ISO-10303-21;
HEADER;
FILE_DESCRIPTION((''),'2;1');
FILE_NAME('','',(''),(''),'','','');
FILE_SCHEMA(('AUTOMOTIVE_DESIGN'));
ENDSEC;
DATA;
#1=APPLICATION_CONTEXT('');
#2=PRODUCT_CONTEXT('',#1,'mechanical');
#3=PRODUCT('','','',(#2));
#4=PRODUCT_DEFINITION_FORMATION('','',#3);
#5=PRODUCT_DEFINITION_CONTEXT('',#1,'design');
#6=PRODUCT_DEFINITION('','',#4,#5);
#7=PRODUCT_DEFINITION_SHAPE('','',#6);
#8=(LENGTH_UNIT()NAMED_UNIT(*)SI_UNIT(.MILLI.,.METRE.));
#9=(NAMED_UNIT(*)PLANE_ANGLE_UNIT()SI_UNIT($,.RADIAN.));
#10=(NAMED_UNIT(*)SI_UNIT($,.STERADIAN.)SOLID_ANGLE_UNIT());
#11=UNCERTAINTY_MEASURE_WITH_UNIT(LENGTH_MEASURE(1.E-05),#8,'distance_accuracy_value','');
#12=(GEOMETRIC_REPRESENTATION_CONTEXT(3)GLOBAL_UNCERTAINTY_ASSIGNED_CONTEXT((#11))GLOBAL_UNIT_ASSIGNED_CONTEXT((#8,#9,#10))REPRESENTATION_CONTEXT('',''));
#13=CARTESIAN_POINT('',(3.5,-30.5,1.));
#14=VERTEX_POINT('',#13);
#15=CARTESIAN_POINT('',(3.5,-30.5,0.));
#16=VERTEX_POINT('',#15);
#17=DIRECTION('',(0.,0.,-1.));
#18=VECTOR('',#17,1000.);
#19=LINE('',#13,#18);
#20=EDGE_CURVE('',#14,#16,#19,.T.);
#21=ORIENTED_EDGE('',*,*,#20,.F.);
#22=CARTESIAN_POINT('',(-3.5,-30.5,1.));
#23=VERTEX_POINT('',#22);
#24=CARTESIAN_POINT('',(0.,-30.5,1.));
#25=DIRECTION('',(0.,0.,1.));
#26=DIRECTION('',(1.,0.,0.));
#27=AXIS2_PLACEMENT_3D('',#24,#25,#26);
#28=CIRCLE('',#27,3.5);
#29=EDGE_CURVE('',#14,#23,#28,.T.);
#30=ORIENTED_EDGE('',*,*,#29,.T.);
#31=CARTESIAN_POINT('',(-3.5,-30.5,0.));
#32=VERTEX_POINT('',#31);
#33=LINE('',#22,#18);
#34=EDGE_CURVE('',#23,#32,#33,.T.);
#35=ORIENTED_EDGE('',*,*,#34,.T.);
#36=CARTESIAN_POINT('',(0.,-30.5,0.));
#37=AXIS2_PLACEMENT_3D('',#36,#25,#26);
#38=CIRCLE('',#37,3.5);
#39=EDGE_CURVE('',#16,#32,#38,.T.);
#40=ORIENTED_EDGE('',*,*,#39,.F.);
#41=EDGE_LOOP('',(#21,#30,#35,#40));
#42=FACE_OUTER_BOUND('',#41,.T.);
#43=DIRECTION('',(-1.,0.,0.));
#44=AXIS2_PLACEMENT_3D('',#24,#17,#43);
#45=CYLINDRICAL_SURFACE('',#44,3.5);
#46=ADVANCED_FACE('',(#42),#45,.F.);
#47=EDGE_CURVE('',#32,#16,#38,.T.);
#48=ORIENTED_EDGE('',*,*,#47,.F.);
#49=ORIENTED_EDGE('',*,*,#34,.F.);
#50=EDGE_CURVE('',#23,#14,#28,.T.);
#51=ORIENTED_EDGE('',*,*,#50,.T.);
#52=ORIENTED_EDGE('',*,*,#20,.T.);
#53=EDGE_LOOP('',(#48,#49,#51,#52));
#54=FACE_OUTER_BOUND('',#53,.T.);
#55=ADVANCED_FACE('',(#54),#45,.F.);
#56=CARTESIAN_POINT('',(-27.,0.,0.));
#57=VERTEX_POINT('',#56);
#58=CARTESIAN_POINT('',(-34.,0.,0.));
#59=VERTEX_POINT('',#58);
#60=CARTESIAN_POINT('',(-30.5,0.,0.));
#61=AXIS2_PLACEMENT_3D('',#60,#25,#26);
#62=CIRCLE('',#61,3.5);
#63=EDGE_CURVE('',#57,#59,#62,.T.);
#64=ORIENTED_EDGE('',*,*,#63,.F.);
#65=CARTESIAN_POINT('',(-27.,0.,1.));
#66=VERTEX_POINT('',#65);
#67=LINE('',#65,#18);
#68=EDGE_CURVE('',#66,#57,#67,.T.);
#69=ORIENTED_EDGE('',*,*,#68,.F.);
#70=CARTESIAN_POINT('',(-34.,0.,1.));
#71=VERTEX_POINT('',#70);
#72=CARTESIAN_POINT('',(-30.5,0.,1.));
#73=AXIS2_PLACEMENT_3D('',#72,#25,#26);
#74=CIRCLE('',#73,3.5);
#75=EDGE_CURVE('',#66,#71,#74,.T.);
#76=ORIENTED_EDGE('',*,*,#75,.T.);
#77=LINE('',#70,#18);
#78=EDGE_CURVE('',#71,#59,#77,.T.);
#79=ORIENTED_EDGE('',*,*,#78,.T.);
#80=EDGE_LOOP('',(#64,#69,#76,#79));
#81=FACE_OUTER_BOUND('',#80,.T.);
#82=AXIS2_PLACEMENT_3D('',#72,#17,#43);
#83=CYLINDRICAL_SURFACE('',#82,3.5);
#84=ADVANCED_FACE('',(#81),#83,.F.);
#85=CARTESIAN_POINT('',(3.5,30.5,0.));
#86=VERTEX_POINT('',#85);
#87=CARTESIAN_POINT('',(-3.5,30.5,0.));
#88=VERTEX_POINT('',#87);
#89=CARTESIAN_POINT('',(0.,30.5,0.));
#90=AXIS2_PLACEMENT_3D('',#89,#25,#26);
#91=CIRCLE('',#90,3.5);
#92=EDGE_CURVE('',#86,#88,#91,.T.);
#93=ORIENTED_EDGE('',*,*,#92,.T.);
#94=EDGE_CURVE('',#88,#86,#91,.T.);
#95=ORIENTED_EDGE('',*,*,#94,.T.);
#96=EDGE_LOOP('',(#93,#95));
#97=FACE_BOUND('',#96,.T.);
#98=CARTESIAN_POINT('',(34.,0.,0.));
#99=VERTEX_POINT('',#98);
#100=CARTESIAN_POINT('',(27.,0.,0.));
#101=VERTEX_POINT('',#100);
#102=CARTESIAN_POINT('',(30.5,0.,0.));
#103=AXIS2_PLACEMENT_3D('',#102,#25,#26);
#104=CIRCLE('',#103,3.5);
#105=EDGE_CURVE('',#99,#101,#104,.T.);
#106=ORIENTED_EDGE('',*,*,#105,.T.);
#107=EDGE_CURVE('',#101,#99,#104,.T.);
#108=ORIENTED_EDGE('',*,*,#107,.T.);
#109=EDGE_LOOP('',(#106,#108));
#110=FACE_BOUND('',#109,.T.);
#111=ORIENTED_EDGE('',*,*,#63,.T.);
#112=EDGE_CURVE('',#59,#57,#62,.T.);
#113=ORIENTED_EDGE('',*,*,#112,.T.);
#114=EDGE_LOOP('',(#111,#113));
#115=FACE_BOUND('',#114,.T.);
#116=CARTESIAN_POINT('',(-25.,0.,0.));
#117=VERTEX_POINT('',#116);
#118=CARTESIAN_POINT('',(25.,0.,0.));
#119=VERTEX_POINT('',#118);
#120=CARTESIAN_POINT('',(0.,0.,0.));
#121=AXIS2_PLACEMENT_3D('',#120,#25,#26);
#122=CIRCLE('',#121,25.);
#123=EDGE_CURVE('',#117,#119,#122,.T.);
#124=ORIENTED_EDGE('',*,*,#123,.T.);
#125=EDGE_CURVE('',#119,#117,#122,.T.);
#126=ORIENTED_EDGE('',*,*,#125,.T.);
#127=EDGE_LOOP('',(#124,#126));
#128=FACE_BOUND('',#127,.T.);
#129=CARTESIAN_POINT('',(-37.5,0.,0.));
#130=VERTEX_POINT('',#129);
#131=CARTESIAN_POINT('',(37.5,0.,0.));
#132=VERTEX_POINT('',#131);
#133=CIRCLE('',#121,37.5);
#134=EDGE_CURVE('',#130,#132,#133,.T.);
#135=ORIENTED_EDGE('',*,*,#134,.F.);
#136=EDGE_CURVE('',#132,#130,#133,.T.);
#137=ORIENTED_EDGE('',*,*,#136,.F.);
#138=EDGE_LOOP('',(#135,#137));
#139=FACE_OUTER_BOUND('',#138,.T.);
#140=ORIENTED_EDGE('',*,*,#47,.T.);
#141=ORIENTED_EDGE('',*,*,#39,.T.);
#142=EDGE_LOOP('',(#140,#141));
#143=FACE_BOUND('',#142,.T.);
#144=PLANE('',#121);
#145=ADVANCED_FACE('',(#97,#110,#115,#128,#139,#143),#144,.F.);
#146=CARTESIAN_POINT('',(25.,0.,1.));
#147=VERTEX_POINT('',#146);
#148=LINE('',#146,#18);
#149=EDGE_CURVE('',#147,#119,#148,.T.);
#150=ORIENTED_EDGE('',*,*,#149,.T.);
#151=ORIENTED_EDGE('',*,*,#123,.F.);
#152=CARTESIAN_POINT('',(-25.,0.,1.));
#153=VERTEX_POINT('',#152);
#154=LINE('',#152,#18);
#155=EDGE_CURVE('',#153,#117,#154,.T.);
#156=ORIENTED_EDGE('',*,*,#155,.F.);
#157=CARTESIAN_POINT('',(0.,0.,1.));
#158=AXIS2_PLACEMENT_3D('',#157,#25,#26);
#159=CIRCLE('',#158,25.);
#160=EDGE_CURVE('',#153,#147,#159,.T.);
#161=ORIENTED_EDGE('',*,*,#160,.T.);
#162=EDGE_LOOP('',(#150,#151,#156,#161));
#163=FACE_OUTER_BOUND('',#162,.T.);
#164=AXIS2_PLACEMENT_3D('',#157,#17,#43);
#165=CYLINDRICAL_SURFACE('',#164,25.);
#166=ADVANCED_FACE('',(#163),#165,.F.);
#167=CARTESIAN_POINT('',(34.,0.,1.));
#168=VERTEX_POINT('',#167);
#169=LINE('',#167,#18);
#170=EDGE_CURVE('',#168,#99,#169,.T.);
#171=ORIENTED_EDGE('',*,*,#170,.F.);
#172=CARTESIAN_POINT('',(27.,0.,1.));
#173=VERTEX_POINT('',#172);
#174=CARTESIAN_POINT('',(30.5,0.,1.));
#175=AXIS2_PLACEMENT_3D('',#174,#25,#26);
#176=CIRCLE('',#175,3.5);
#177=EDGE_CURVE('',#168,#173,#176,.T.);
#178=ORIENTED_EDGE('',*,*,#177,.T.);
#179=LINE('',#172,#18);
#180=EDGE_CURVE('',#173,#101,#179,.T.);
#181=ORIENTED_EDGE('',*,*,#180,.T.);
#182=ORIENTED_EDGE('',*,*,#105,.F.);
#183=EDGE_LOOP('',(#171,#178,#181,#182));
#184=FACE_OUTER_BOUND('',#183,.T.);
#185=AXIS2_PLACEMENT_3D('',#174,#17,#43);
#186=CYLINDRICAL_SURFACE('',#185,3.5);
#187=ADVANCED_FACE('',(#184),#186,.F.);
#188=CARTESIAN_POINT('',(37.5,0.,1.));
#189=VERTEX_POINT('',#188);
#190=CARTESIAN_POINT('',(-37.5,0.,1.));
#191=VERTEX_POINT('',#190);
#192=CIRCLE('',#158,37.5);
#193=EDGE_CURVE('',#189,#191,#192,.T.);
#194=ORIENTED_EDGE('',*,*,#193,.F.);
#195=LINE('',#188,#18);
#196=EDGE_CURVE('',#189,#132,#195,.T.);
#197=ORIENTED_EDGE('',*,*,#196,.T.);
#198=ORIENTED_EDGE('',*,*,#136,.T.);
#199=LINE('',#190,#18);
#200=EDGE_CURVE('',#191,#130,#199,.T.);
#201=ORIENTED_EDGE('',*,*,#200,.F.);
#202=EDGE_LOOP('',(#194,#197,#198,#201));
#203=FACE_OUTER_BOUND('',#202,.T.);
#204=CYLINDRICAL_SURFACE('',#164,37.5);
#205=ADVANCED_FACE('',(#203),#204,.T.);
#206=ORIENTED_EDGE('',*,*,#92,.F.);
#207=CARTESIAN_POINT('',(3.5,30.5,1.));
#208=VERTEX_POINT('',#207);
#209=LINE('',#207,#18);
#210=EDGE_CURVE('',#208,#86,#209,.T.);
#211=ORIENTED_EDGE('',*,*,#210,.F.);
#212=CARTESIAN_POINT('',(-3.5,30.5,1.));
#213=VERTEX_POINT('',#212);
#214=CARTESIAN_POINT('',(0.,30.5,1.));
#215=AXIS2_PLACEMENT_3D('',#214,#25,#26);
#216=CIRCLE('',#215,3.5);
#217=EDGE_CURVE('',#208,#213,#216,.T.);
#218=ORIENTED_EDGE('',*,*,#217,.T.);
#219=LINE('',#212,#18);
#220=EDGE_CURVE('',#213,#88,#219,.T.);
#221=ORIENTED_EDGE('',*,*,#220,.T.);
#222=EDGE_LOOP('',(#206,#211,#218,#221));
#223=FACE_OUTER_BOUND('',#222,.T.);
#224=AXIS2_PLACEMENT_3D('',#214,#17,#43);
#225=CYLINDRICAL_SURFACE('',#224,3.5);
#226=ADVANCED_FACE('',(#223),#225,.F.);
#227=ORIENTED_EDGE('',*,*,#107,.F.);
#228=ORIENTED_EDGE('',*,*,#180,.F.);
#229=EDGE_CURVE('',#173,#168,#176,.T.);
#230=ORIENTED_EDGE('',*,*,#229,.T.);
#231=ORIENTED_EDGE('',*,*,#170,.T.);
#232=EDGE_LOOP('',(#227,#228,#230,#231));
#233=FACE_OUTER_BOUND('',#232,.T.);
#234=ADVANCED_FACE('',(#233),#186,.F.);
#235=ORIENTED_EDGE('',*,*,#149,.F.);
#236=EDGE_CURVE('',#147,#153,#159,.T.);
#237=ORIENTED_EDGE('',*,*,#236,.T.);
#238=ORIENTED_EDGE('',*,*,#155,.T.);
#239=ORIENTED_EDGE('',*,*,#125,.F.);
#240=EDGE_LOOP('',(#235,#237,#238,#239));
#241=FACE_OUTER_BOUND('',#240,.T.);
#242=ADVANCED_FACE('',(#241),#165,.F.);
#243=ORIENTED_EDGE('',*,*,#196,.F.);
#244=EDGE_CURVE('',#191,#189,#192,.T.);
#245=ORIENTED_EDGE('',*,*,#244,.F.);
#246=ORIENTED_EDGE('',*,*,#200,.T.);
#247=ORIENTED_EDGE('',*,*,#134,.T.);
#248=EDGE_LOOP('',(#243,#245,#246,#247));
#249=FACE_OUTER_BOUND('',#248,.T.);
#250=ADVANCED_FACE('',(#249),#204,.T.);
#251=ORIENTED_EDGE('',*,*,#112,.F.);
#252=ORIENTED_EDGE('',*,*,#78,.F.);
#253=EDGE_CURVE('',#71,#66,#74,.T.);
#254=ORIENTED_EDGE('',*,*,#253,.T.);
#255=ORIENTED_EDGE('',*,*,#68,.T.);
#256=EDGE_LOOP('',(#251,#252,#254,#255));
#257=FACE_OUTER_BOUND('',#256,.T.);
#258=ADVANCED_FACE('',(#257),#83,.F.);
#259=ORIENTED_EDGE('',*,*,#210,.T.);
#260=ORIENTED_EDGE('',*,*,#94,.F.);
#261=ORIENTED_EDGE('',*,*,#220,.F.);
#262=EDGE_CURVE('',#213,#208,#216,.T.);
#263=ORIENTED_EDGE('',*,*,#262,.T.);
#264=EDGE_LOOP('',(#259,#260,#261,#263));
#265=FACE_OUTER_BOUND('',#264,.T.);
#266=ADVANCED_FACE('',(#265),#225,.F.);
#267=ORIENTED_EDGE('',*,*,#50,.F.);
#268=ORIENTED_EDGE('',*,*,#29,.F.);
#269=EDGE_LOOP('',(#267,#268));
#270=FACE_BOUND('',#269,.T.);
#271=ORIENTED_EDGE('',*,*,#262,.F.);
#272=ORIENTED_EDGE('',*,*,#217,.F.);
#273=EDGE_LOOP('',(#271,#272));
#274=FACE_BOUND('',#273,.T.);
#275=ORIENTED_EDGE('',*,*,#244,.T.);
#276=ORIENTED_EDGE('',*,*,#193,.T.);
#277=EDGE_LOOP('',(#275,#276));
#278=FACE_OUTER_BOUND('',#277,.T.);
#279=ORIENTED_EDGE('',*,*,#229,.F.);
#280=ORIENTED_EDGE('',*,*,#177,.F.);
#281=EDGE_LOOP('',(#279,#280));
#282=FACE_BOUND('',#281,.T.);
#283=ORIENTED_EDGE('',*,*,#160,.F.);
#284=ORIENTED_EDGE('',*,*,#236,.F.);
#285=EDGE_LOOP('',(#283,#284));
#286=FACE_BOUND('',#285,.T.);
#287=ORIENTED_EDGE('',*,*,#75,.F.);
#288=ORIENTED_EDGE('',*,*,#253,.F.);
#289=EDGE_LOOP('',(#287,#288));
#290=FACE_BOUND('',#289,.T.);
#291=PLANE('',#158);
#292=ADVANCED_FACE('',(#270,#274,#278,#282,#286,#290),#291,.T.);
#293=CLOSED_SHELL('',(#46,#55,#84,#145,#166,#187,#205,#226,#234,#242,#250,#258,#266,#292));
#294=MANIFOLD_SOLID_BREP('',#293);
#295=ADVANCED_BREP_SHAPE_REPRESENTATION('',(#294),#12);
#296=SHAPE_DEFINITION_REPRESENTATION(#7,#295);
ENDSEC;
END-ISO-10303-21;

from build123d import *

# Parameters (mm, degrees)
SKETCH1_R           = 37.5
SKETCH1_R_2         = 25
SKETCH1_R_3         = 3.5
BOSS_EXTRUDE1_DEPTH = 1


with BuildPart() as part:
    # Sketch1 → Boss-Extrude1 (new body)
    with BuildSketch(Plane.XY):
        Circle(SKETCH1_R)
        Circle(SKETCH1_R_2, mode=Mode.SUBTRACT)
        with Locations((0, 30.5)):
            Circle(SKETCH1_R_3, mode=Mode.SUBTRACT)
        with Locations((30.5, 0)):
            Circle(SKETCH1_R_3, mode=Mode.SUBTRACT)
        with Locations((0, -30.5)):
            Circle(SKETCH1_R_3, mode=Mode.SUBTRACT)
        with Locations((-30.5, 0)):
            Circle(SKETCH1_R_3, mode=Mode.SUBTRACT)
    extrude(amount=BOSS_EXTRUDE1_DEPTH)


solid = part.part
